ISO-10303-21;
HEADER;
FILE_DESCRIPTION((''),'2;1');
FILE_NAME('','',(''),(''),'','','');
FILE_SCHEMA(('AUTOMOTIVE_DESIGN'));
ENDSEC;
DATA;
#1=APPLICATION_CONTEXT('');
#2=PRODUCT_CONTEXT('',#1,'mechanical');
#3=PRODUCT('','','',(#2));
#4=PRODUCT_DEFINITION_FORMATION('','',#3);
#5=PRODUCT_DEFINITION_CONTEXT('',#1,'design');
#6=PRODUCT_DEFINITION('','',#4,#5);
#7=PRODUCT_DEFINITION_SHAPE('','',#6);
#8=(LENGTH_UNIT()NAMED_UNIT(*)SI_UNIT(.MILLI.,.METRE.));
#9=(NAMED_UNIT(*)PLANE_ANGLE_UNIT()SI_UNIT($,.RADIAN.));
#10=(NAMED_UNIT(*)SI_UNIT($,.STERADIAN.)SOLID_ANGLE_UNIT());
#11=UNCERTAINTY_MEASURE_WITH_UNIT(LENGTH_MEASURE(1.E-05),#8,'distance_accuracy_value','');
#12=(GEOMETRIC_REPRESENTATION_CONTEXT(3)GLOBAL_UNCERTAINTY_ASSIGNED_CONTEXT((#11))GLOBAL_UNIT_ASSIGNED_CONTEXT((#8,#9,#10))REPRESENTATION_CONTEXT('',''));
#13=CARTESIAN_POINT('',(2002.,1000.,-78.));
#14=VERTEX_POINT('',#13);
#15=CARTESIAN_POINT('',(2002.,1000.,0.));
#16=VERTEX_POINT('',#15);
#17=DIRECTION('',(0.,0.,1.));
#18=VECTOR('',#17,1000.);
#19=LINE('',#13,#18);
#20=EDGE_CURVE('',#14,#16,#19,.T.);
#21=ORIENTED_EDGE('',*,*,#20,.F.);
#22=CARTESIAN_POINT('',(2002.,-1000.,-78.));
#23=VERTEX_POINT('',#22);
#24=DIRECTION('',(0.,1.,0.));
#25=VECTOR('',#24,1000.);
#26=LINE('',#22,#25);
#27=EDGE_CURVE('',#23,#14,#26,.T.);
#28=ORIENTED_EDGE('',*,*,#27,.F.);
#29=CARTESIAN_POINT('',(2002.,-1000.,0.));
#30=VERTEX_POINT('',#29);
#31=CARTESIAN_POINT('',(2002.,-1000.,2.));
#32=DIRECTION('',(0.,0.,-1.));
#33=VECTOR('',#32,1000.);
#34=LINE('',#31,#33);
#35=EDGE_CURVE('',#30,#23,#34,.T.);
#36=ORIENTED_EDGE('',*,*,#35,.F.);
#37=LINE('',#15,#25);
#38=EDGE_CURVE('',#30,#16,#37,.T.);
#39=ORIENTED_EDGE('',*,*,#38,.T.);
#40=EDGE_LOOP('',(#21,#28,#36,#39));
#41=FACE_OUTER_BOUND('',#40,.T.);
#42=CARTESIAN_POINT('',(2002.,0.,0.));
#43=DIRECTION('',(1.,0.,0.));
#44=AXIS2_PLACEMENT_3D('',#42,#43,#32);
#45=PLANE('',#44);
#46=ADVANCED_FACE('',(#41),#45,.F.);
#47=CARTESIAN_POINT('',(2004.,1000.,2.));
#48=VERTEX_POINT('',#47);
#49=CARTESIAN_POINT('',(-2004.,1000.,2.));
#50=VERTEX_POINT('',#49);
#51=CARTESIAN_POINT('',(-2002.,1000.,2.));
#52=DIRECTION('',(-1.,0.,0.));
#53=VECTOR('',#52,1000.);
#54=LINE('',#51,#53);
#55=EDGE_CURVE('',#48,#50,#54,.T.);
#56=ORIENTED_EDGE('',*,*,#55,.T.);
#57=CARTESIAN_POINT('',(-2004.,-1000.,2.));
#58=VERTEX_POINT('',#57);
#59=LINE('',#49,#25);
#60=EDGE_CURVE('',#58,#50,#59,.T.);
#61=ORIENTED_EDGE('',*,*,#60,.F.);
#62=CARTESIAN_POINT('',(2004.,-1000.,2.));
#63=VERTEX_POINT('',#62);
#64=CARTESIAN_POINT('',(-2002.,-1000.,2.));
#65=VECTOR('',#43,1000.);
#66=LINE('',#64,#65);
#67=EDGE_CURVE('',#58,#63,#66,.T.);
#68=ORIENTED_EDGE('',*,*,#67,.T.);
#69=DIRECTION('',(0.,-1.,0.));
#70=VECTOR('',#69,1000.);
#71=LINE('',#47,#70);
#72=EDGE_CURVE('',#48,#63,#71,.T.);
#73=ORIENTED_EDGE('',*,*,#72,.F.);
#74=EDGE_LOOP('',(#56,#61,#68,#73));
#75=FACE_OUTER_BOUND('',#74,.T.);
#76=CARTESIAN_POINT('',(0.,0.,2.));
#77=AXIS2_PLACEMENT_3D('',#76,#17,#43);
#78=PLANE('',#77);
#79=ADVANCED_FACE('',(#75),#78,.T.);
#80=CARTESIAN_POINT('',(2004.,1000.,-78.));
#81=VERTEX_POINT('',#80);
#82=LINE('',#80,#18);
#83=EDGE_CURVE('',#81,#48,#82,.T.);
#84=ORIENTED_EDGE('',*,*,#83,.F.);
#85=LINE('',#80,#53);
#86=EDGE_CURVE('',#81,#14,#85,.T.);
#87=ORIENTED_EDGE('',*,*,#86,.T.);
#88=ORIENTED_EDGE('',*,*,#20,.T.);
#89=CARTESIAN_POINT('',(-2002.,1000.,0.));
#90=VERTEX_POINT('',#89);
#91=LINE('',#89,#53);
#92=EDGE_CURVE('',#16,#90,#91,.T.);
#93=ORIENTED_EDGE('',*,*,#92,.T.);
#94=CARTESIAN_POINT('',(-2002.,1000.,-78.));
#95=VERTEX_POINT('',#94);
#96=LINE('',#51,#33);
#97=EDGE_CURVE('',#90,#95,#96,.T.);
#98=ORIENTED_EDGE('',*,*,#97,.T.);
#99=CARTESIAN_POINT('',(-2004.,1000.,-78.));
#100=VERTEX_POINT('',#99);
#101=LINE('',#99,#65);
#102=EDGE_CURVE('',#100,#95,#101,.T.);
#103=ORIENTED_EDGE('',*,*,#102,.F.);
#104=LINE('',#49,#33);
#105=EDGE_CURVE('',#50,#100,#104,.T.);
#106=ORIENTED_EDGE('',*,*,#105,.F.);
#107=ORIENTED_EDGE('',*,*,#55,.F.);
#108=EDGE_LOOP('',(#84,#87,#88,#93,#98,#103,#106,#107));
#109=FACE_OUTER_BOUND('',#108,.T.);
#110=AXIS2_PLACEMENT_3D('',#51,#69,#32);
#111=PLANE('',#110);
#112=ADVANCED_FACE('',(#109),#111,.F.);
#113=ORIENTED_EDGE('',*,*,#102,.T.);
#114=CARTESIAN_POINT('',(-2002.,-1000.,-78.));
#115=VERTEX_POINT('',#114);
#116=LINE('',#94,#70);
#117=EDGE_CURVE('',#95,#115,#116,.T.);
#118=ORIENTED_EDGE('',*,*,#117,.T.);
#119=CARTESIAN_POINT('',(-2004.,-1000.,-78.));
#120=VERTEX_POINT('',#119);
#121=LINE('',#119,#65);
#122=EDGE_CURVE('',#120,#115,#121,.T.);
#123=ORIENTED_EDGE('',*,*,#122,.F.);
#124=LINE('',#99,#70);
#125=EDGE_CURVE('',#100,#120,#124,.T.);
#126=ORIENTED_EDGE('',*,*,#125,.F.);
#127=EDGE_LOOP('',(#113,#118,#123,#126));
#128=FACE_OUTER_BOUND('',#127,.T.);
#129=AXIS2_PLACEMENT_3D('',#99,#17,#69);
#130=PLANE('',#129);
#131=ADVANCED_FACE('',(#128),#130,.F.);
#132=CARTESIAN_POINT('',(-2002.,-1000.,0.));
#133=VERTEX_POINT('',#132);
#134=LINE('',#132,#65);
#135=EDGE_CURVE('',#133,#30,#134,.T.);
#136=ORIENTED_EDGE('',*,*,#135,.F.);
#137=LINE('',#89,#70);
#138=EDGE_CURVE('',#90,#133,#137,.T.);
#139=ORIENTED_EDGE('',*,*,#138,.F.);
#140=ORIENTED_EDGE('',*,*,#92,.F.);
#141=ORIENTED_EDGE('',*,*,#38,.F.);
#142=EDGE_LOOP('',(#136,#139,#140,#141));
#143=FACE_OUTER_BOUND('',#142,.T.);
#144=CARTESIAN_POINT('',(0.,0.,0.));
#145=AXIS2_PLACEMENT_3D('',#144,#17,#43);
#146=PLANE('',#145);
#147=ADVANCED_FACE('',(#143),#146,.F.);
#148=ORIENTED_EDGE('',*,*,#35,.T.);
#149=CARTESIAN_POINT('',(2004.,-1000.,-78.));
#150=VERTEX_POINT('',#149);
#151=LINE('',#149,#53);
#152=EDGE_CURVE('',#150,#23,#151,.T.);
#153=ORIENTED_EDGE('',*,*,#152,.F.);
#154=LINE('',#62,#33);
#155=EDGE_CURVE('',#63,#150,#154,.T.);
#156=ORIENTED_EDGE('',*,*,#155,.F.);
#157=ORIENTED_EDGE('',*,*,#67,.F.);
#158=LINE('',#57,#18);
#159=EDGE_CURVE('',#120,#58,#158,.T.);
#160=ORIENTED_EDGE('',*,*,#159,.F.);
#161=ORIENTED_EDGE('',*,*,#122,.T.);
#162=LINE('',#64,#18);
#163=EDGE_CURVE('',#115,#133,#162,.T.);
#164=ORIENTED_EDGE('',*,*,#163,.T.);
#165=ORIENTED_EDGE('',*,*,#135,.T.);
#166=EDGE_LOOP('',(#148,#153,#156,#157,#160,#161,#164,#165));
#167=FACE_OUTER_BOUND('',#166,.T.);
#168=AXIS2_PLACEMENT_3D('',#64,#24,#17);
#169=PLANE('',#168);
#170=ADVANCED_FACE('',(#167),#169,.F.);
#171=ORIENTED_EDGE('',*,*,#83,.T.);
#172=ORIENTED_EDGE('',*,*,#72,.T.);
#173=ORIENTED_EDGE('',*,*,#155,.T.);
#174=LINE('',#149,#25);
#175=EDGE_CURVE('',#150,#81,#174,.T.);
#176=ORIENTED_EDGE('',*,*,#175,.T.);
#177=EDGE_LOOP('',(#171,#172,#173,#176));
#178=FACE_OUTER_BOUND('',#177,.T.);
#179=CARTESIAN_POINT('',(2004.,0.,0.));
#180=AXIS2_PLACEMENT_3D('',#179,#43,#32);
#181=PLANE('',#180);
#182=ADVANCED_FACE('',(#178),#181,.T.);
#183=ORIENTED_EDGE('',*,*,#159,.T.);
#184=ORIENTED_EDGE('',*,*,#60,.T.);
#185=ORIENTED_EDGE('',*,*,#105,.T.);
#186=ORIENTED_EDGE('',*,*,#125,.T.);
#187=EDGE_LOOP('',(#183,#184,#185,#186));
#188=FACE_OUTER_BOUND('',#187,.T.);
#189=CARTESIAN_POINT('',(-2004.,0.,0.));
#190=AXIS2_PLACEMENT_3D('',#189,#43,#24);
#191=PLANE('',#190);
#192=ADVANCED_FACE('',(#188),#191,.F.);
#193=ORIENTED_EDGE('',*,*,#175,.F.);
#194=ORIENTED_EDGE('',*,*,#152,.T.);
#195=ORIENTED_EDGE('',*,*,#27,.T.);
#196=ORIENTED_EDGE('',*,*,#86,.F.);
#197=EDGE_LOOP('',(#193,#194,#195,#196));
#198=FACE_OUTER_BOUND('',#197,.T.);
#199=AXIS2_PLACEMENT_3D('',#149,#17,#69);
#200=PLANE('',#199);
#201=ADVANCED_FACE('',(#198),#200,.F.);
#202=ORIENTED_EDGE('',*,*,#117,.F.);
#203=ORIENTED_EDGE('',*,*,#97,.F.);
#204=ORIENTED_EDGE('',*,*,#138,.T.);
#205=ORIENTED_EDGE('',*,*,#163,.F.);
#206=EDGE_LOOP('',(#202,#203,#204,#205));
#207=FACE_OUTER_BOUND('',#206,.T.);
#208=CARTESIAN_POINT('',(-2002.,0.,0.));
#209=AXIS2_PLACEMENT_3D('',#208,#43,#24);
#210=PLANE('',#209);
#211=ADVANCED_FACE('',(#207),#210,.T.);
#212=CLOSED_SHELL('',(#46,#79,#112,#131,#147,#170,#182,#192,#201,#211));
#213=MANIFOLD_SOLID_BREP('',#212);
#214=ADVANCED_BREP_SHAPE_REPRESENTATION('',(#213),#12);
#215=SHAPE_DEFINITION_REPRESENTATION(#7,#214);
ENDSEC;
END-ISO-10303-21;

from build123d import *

# Parameters (mm, degrees)
SKETCH_1_W      = 4004
SKETCH_1_H      = 2000
EXTRUDE_1_DEPTH = 2
SKETCH_2_W      = 80
SKETCH_2_H      = 2000
EXTRUDE_2_DEPTH = 2
SKETCH_3_W      = 80
SKETCH_3_H      = 2000
EXTRUDE_3_DEPTH = 2


with BuildPart() as part:
    # 草图1 → 凸台-拉伸1 (new body)
    with BuildSketch(Plane.XY):
        Rectangle(SKETCH_1_W, SKETCH_1_H)
    extrude(amount=EXTRUDE_1_DEPTH)

    # 草图2 → 凸台-拉伸2 (add)
    with BuildSketch(Plane.ZY.offset(2002)):
        with Locations((-38, 0)):
            Rectangle(SKETCH_2_W, SKETCH_2_H)
    extrude(amount=EXTRUDE_2_DEPTH)

    # 草图3 → 凸台-拉伸3 (add)
    with BuildSketch(Plane(origin=(2002, 0, 0), x_dir=(0, 0, -1), z_dir=(1, 0, 0))):
        with Locations((38, 0)):
            Rectangle(SKETCH_3_W, SKETCH_3_H)
    extrude(amount=EXTRUDE_3_DEPTH)


solid = part.part
